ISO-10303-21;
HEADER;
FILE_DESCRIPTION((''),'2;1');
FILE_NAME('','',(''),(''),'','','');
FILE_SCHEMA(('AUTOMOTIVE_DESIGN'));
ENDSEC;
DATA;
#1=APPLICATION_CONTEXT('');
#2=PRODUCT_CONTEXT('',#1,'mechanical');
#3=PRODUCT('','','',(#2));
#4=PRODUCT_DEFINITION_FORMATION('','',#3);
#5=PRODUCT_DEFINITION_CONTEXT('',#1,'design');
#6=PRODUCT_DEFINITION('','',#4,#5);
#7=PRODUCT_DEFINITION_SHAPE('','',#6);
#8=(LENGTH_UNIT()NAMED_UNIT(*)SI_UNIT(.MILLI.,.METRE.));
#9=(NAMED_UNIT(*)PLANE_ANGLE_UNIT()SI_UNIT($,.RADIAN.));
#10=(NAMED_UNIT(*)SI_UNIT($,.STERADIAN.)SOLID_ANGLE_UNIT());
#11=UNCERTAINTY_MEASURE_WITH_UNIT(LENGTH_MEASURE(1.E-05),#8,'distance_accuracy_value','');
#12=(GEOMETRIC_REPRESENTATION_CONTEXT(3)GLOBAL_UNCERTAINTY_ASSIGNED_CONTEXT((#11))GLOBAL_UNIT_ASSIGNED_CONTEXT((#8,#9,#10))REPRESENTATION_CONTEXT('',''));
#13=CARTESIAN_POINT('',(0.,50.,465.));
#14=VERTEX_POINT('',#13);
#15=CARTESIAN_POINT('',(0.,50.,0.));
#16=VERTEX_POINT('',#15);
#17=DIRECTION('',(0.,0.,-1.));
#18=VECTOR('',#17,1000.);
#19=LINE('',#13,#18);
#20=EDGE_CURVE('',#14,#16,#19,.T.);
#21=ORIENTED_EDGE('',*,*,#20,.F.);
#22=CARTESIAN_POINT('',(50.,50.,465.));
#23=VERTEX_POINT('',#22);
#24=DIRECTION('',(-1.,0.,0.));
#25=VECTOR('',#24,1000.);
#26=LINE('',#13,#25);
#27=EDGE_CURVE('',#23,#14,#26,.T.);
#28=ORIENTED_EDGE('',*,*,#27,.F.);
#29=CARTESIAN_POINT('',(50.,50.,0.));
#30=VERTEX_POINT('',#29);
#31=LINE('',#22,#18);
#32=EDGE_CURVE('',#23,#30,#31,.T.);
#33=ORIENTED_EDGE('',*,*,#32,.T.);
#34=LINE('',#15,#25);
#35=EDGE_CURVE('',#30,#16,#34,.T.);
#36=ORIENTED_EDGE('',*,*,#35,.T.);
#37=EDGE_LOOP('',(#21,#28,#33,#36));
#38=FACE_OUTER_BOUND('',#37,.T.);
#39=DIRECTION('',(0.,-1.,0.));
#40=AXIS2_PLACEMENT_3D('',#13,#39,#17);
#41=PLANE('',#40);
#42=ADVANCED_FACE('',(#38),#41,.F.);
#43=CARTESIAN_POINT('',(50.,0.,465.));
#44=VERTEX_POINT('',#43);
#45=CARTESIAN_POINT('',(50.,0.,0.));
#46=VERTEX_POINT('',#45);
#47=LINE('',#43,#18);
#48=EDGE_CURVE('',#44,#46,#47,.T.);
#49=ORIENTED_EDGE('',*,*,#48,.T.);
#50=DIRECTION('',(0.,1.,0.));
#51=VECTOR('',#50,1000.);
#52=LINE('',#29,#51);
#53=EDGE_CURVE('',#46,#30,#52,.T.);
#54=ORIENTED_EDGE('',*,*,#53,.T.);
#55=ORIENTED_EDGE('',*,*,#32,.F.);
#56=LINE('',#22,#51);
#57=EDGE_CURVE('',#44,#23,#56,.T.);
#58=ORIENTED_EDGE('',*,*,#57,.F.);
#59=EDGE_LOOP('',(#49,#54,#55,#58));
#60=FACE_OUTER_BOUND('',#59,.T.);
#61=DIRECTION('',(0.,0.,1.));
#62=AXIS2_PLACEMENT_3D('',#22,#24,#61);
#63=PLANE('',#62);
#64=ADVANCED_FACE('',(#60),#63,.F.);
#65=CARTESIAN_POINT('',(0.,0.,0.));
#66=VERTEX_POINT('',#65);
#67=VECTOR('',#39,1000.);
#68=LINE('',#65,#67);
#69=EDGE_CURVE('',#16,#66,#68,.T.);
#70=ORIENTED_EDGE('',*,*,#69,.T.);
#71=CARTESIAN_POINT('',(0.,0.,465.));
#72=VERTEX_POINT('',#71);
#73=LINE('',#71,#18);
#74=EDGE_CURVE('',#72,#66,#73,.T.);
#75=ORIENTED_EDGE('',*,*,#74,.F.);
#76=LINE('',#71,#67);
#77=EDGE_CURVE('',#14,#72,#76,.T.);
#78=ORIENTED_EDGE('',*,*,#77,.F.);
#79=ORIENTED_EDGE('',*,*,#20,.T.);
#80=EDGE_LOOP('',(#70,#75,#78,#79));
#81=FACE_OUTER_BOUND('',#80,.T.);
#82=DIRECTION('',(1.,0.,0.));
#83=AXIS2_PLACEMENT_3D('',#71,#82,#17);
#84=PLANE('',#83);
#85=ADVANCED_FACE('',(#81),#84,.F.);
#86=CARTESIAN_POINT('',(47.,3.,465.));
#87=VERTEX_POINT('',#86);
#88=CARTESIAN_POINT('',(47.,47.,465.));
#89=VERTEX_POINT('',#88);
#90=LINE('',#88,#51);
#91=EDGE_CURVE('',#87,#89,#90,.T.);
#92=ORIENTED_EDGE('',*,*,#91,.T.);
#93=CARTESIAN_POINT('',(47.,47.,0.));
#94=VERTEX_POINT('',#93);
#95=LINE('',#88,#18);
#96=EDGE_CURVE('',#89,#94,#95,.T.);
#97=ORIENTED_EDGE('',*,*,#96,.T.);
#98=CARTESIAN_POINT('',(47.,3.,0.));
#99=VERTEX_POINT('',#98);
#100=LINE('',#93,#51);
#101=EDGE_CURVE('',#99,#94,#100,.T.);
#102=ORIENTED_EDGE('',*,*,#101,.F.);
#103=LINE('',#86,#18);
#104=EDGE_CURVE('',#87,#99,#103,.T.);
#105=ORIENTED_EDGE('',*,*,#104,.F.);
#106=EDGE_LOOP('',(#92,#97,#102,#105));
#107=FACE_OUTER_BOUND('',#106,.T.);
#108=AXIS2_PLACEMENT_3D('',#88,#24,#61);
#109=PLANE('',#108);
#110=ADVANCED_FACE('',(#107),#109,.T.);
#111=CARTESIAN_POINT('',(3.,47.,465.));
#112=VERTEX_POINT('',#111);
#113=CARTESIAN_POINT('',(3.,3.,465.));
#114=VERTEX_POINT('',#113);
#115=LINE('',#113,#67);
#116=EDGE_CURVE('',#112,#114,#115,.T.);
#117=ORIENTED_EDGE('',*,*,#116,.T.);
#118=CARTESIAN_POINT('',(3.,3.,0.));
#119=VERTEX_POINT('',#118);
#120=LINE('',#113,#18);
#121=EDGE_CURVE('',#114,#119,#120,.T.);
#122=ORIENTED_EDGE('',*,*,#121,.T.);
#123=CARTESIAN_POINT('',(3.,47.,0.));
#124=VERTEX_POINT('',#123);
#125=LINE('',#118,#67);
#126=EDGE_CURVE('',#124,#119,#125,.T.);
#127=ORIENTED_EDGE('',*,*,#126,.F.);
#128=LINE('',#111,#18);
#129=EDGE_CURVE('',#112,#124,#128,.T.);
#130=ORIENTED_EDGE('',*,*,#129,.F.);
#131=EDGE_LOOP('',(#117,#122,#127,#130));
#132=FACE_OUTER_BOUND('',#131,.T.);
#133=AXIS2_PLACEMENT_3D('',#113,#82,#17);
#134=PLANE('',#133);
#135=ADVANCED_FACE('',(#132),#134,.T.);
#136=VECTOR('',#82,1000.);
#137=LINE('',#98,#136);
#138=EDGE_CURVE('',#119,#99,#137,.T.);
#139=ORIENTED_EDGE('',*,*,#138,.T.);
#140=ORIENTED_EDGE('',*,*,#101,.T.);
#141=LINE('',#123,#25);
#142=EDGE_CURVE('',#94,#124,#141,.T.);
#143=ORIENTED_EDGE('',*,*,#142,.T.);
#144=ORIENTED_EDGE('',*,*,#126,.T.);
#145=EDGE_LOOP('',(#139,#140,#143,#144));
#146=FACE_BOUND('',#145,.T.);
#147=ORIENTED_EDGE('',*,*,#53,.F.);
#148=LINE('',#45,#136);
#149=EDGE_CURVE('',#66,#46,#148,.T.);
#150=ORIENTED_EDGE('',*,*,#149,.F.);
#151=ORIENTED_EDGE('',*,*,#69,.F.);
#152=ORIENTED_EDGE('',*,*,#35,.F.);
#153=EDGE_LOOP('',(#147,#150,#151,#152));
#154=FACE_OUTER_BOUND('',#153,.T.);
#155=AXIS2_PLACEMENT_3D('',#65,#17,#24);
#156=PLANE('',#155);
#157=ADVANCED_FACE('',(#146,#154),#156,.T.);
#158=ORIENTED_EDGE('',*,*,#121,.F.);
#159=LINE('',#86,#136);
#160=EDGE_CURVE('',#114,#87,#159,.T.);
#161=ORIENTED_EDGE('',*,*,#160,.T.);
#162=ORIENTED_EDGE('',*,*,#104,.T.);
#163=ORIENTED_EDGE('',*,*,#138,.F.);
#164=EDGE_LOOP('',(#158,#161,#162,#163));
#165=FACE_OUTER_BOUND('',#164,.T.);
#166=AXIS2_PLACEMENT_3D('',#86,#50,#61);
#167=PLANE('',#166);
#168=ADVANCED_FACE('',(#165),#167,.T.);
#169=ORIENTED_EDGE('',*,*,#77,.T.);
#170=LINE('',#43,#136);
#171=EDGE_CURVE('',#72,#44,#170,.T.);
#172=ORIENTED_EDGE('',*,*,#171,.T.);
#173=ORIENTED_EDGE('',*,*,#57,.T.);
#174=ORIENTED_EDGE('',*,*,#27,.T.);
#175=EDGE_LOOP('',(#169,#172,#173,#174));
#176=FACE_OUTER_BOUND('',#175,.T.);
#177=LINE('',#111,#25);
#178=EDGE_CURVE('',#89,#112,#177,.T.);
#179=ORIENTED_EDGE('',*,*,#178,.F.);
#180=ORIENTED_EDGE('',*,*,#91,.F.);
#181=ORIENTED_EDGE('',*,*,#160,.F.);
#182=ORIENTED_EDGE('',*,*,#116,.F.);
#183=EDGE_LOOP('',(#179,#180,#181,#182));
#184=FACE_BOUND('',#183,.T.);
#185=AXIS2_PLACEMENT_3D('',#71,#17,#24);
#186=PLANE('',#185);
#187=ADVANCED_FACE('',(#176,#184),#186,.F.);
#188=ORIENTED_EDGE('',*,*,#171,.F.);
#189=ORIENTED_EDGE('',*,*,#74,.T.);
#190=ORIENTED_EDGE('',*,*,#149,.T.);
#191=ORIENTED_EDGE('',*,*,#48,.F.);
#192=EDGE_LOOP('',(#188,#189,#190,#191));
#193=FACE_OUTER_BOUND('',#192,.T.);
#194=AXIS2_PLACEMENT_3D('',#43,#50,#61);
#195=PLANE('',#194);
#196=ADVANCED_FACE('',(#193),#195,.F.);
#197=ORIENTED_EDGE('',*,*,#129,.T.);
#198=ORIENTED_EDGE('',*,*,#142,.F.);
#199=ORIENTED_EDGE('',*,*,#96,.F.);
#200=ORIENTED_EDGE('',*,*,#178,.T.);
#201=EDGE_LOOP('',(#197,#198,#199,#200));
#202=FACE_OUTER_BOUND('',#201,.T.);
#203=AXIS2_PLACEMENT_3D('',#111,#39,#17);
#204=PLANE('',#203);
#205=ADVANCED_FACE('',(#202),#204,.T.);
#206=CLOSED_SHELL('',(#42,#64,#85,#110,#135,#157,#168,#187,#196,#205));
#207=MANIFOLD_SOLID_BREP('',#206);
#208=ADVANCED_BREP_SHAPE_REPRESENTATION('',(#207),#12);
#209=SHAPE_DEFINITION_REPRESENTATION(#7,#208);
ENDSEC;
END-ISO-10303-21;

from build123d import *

# Parameters (mm, degrees)
SKETCH_1_W      = 50
SKETCH_1_H      = 50
SKETCH_1_W_2    = 44
SKETCH_1_H_2    = 44
EXTRUDE_1_DEPTH = 465


with BuildPart() as part:
    # 草图1 → 凸台-拉伸1 (new body)
    with BuildSketch(Plane.XY):
        with Locations((25, 25)):
            Rectangle(SKETCH_1_W, SKETCH_1_H)
        with Locations((25, 25)):
            Rectangle(SKETCH_1_W_2, SKETCH_1_H_2, mode=Mode.SUBTRACT)
    extrude(amount=EXTRUDE_1_DEPTH)


solid = part.part
